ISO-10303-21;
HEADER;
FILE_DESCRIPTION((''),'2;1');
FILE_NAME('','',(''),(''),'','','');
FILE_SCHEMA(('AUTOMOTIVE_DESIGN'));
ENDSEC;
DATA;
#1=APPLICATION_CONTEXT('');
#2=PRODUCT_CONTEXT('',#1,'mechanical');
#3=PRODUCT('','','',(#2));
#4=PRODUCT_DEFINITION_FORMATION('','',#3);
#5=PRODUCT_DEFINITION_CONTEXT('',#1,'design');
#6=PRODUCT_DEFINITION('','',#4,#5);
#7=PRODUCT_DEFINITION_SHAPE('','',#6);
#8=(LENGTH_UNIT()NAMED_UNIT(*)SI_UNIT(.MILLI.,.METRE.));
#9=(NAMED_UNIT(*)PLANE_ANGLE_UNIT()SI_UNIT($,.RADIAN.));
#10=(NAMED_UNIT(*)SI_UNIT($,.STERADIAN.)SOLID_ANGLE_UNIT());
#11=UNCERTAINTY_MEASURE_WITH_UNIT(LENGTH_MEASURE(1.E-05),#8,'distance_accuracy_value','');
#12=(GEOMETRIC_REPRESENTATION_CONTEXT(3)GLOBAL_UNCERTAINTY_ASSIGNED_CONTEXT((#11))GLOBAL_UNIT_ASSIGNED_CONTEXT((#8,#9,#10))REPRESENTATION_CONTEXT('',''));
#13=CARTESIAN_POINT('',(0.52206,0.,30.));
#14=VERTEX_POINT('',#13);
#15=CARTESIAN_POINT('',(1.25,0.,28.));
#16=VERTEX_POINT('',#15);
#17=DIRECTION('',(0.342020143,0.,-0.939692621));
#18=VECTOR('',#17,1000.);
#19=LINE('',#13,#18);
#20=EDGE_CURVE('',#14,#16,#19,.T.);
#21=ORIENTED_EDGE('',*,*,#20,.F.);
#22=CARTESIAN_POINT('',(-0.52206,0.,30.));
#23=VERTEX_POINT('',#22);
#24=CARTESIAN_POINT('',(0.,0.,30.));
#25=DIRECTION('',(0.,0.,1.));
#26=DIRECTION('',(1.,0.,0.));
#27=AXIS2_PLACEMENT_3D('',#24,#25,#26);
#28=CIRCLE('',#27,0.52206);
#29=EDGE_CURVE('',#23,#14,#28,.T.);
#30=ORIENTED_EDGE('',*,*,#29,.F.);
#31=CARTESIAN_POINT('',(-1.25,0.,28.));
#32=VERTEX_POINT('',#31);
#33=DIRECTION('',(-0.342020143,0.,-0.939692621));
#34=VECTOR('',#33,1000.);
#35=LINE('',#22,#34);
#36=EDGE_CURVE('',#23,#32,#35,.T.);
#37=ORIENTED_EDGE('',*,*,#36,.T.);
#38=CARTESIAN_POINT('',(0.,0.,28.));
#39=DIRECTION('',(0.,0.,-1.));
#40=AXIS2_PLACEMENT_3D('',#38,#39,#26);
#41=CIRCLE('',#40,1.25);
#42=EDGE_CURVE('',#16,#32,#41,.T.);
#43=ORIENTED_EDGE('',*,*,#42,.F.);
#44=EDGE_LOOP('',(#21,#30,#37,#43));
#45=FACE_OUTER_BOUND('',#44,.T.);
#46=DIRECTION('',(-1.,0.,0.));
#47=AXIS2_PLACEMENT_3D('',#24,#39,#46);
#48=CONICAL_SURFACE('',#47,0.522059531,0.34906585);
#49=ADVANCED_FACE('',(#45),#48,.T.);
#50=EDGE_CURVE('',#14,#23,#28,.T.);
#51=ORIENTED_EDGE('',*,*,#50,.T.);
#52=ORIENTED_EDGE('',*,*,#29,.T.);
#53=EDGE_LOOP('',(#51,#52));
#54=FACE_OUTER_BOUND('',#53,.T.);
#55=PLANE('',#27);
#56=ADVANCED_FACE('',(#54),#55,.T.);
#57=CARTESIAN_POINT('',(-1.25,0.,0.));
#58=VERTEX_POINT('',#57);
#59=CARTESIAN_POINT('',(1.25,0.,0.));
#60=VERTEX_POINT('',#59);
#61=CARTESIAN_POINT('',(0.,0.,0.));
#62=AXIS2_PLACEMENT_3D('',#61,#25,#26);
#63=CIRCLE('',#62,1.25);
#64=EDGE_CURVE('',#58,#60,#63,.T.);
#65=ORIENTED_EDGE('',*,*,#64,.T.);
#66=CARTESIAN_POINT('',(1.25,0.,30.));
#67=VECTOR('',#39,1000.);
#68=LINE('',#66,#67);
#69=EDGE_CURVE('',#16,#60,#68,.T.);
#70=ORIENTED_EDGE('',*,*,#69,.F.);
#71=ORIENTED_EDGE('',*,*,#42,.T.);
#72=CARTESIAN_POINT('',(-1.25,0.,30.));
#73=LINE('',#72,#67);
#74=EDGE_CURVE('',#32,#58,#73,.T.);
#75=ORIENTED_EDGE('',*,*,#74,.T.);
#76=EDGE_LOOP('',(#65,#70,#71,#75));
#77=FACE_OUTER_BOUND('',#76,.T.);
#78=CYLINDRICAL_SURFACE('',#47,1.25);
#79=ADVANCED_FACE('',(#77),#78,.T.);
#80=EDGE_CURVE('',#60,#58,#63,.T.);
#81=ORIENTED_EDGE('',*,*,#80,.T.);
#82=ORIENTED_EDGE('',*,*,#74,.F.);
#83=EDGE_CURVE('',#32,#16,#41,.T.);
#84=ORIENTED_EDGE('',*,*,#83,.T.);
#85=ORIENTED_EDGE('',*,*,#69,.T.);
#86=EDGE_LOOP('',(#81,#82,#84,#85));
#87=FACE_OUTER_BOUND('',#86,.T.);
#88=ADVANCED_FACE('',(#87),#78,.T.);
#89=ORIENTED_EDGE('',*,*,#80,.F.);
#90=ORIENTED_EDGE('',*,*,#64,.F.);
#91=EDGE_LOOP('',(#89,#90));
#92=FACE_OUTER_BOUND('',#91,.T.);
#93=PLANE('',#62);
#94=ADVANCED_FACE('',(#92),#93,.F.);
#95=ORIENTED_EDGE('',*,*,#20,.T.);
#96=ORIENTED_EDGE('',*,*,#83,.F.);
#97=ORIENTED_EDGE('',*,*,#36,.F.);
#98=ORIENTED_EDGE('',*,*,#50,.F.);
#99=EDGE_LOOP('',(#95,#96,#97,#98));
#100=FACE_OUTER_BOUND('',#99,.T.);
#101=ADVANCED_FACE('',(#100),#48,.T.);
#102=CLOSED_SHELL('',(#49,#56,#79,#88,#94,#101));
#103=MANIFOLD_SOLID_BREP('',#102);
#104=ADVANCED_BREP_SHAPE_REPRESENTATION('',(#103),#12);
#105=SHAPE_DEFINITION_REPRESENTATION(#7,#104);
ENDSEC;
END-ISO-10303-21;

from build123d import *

# Parameters (mm, degrees)
SKETCH_1_R      = 1.25
EXTRUDE_1_DEPTH = 30
CHAMFER_1_SIZE  = 2
CHAMFER_1_SIZE2 = 0.727940469


with BuildPart() as part:
    # 草图1 → 凸台-拉伸1 (new body)
    with BuildSketch(Plane.XY):
        Circle(SKETCH_1_R)
    extrude(amount=EXTRUDE_1_DEPTH)

    # 倒角1
    chamfer_1_edges = [part.edges().sort_by_distance(p)[0] for p in [
        (-1.25, 0, 30),
    ]]
    chamfer_1_side = [part.faces().sort_by_distance(p)[0] for p in [
        (-1.25, 0, 15),
    ]]
    chamfer(chamfer_1_edges, length=CHAMFER_1_SIZE, length2=CHAMFER_1_SIZE2, reference=chamfer_1_side[0])


solid = part.part
